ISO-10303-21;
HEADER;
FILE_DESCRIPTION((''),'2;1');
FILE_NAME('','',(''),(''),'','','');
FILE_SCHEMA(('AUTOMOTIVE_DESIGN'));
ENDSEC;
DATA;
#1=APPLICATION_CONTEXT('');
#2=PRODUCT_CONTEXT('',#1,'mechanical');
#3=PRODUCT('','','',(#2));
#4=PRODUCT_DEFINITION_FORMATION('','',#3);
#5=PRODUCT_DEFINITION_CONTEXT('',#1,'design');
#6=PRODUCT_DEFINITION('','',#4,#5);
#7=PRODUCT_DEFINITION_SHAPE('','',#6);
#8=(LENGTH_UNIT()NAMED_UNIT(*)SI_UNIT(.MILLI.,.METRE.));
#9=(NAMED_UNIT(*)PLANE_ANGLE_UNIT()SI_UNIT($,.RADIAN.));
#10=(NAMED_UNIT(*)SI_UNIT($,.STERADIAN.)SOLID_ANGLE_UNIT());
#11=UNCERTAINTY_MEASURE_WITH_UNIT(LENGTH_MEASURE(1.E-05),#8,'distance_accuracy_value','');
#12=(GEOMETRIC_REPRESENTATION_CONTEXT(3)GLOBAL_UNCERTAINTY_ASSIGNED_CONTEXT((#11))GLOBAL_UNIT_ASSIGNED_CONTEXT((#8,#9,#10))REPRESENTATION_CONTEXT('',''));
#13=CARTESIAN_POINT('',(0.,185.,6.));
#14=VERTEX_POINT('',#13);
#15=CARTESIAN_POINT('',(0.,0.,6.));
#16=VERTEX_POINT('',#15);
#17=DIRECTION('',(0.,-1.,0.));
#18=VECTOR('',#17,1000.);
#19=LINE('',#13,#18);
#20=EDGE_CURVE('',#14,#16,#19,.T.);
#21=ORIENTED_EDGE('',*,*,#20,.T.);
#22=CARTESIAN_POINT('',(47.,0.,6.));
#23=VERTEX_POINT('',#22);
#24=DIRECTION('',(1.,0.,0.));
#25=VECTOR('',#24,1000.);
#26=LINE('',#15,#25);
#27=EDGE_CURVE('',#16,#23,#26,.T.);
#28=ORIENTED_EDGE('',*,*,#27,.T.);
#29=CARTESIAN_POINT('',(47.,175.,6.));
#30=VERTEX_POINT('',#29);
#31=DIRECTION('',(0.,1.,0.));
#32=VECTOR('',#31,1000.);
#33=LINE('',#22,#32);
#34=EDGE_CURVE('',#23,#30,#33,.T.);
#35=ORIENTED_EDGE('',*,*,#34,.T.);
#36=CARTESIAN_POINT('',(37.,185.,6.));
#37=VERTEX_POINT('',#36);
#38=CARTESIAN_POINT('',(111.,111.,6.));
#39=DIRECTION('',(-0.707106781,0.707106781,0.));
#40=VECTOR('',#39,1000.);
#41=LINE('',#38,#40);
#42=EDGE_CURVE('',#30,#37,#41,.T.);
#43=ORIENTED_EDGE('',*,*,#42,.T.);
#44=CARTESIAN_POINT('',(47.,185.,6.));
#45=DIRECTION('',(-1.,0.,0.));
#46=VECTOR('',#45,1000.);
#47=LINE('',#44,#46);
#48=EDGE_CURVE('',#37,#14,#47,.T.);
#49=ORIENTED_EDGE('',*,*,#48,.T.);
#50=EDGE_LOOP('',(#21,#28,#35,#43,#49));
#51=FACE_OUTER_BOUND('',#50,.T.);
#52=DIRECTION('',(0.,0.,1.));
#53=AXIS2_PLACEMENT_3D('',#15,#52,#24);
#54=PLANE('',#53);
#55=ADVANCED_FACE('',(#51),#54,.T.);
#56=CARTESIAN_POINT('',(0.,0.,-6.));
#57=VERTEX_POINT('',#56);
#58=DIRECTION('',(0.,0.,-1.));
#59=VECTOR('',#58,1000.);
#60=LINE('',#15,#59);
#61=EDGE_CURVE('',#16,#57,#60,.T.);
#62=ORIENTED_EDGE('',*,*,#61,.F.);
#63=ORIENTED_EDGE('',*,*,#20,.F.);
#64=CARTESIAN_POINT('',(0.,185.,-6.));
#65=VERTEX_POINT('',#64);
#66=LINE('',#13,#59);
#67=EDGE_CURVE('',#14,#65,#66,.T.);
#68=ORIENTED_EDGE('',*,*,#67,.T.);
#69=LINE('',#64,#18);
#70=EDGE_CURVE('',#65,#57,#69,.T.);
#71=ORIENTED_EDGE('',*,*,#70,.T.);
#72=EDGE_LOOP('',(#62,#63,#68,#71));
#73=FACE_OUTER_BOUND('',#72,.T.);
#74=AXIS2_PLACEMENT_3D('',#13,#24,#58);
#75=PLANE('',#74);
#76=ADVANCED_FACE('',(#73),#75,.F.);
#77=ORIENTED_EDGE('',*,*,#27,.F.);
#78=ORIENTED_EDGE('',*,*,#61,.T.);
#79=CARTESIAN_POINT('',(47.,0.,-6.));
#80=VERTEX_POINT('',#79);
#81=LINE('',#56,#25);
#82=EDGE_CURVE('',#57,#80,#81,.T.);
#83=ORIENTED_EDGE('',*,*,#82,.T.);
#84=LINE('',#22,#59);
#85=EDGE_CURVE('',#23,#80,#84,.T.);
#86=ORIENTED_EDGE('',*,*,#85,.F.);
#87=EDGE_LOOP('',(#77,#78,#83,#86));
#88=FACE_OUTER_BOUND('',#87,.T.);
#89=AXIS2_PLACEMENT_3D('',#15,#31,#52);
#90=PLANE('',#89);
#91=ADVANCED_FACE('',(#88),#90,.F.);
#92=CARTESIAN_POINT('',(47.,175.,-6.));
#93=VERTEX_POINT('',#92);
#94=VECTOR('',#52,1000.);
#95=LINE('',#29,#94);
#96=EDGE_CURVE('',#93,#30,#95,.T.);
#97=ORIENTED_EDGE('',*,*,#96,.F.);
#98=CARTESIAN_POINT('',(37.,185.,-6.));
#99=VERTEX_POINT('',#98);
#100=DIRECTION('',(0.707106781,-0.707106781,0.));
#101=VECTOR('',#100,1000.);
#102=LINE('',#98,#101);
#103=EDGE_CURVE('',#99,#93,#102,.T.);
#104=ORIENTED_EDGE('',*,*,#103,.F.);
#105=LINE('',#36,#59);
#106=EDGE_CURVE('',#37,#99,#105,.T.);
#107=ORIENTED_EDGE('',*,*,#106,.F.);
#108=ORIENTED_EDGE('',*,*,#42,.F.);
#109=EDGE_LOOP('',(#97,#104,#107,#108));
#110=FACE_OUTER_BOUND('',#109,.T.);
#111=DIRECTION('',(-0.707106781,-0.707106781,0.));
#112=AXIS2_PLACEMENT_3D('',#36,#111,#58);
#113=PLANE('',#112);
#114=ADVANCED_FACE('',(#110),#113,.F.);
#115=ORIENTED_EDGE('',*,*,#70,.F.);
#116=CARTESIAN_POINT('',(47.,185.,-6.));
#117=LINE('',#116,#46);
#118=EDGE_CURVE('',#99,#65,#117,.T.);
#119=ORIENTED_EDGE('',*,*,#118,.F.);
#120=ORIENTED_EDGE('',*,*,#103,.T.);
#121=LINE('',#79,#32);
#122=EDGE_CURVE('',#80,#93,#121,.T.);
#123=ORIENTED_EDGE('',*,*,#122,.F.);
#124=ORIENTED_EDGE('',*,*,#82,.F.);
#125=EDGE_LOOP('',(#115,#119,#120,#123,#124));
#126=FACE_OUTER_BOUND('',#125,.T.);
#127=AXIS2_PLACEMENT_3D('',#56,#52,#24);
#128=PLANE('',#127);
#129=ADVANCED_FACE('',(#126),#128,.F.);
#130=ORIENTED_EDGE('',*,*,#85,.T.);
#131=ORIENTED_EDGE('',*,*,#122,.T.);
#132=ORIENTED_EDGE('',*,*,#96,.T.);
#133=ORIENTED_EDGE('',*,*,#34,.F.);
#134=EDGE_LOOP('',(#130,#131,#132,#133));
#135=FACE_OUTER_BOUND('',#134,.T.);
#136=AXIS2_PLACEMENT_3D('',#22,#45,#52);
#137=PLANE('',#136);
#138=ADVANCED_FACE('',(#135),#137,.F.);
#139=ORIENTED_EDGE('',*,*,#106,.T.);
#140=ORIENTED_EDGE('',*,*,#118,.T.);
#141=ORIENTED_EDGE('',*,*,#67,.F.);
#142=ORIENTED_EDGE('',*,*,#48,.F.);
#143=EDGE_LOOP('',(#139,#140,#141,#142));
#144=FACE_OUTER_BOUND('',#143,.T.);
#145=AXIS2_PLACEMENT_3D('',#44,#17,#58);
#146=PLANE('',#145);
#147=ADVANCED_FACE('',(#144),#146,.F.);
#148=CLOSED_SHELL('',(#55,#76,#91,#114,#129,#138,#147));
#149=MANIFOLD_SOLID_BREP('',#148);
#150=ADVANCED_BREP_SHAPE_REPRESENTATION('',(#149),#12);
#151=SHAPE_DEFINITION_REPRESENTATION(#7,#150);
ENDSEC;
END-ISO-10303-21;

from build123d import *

# Parameters (mm, degrees)
SKETCH_1_W      = 47
SKETCH_1_H      = 185
EXTRUDE_1_DEPTH = 6
CHAMFER_1_SIZE  = 10


with BuildPart() as part:
    # 草图1 → 凸台-拉伸1 (new, symmetric)
    with BuildSketch(Plane.XY):
        with Locations((23.5, 92.5)):
            Rectangle(SKETCH_1_W, SKETCH_1_H)
    extrude(amount=EXTRUDE_1_DEPTH, both=True)

    # 倒角1
    chamfer_1_edges = [part.edges().sort_by_distance(p)[0] for p in [
        (47, 185, 0),
    ]]
    chamfer(chamfer_1_edges, length=CHAMFER_1_SIZE)


solid = part.part
